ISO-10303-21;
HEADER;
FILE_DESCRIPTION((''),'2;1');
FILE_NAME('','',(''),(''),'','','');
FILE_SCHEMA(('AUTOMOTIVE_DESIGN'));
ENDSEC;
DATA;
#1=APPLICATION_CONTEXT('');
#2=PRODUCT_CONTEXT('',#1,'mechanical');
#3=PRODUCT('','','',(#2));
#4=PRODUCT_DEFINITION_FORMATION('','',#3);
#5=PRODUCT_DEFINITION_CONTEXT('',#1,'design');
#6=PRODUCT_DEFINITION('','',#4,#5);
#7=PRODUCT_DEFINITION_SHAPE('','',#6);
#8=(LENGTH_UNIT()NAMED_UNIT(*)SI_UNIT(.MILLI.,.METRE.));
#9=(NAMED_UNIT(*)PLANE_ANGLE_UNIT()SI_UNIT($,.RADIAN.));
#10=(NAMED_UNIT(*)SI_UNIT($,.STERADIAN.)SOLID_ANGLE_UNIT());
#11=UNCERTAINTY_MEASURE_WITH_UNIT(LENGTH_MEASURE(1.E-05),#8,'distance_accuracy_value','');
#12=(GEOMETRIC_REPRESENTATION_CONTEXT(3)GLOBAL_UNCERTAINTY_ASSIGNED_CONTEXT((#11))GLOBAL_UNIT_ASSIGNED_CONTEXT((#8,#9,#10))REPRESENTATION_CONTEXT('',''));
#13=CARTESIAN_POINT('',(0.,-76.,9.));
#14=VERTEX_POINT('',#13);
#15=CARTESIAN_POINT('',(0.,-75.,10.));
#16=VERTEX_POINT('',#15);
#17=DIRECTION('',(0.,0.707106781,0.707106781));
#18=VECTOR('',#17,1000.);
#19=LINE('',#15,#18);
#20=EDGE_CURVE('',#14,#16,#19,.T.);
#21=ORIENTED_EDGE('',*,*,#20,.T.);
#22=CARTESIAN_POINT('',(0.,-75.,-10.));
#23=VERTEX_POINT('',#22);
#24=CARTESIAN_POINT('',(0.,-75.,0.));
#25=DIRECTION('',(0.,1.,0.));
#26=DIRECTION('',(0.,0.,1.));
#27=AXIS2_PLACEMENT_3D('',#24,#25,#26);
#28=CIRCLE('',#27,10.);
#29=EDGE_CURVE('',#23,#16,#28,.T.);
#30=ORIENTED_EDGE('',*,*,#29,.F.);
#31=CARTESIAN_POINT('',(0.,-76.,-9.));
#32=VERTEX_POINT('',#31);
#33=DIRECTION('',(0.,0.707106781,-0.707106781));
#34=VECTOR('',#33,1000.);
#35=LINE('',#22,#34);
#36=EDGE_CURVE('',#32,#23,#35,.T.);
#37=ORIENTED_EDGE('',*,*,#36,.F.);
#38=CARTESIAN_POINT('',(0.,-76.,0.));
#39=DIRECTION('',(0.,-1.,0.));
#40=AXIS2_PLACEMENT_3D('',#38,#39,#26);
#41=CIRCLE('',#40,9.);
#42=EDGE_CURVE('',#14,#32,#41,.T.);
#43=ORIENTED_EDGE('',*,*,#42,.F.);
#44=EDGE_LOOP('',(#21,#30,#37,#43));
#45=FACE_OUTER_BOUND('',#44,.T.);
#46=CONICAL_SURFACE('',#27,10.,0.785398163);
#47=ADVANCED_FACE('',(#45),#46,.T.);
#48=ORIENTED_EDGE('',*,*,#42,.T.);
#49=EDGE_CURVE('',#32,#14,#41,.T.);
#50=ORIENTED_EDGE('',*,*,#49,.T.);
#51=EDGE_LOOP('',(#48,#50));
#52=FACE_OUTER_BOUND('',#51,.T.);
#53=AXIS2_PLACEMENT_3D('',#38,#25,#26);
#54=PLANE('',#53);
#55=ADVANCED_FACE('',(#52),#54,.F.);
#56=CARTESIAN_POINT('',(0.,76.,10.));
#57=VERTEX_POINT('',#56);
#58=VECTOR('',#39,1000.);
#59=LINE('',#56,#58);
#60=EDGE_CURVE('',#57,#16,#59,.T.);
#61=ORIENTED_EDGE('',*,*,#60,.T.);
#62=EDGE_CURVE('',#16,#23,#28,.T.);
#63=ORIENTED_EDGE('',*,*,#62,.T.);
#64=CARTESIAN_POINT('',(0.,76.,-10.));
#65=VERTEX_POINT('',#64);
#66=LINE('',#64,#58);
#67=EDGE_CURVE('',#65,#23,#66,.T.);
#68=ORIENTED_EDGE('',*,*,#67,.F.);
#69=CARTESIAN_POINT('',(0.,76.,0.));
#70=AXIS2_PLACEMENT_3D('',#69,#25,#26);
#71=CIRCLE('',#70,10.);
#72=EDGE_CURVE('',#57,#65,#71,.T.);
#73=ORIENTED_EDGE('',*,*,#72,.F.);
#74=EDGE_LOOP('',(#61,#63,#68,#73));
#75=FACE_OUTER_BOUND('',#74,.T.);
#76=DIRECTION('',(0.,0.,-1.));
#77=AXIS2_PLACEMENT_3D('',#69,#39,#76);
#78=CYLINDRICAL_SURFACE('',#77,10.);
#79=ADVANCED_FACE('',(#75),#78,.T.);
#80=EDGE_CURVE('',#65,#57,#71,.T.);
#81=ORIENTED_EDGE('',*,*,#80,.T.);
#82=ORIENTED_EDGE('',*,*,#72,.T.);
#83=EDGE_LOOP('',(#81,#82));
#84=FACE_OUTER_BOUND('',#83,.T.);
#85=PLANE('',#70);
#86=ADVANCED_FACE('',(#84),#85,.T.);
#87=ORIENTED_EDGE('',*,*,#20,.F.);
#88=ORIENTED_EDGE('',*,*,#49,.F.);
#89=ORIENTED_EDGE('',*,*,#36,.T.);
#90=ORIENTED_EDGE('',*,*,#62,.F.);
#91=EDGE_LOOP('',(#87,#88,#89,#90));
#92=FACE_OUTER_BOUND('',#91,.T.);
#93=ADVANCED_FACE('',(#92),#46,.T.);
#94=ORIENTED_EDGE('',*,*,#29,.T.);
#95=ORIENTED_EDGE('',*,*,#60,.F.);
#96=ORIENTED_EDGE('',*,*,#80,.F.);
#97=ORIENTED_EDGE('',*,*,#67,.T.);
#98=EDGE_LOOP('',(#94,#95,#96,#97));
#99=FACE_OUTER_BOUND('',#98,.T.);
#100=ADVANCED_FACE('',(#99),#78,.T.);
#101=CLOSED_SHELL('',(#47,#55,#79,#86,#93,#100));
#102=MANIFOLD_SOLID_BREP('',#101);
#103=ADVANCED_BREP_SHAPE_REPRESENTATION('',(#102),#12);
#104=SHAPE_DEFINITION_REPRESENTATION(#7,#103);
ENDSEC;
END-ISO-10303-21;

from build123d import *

# Parameters (mm, degrees)
SKETCH1_R           = 10
BOSS_EXTRUDE1_DEPTH = 76
CHAMFER1_SIZE       = 1


with BuildPart() as part:
    # Sketch1 → Boss-Extrude1 (new, symmetric)
    with BuildSketch(Plane(origin=(0, 0, 0), x_dir=(1, 0, 0), z_dir=(0, 1, 0))):
        with Locations(Location((0, 0, 0), (0, 0, 270))):
            Circle(SKETCH1_R)
    extrude(amount=BOSS_EXTRUDE1_DEPTH, both=True)

    # Chamfer1
    chamfer1_edges = [part.edges().sort_by_distance(p)[0] for p in [
        (0, -76, -10),
    ]]
    chamfer(chamfer1_edges, length=CHAMFER1_SIZE)


solid = part.part
